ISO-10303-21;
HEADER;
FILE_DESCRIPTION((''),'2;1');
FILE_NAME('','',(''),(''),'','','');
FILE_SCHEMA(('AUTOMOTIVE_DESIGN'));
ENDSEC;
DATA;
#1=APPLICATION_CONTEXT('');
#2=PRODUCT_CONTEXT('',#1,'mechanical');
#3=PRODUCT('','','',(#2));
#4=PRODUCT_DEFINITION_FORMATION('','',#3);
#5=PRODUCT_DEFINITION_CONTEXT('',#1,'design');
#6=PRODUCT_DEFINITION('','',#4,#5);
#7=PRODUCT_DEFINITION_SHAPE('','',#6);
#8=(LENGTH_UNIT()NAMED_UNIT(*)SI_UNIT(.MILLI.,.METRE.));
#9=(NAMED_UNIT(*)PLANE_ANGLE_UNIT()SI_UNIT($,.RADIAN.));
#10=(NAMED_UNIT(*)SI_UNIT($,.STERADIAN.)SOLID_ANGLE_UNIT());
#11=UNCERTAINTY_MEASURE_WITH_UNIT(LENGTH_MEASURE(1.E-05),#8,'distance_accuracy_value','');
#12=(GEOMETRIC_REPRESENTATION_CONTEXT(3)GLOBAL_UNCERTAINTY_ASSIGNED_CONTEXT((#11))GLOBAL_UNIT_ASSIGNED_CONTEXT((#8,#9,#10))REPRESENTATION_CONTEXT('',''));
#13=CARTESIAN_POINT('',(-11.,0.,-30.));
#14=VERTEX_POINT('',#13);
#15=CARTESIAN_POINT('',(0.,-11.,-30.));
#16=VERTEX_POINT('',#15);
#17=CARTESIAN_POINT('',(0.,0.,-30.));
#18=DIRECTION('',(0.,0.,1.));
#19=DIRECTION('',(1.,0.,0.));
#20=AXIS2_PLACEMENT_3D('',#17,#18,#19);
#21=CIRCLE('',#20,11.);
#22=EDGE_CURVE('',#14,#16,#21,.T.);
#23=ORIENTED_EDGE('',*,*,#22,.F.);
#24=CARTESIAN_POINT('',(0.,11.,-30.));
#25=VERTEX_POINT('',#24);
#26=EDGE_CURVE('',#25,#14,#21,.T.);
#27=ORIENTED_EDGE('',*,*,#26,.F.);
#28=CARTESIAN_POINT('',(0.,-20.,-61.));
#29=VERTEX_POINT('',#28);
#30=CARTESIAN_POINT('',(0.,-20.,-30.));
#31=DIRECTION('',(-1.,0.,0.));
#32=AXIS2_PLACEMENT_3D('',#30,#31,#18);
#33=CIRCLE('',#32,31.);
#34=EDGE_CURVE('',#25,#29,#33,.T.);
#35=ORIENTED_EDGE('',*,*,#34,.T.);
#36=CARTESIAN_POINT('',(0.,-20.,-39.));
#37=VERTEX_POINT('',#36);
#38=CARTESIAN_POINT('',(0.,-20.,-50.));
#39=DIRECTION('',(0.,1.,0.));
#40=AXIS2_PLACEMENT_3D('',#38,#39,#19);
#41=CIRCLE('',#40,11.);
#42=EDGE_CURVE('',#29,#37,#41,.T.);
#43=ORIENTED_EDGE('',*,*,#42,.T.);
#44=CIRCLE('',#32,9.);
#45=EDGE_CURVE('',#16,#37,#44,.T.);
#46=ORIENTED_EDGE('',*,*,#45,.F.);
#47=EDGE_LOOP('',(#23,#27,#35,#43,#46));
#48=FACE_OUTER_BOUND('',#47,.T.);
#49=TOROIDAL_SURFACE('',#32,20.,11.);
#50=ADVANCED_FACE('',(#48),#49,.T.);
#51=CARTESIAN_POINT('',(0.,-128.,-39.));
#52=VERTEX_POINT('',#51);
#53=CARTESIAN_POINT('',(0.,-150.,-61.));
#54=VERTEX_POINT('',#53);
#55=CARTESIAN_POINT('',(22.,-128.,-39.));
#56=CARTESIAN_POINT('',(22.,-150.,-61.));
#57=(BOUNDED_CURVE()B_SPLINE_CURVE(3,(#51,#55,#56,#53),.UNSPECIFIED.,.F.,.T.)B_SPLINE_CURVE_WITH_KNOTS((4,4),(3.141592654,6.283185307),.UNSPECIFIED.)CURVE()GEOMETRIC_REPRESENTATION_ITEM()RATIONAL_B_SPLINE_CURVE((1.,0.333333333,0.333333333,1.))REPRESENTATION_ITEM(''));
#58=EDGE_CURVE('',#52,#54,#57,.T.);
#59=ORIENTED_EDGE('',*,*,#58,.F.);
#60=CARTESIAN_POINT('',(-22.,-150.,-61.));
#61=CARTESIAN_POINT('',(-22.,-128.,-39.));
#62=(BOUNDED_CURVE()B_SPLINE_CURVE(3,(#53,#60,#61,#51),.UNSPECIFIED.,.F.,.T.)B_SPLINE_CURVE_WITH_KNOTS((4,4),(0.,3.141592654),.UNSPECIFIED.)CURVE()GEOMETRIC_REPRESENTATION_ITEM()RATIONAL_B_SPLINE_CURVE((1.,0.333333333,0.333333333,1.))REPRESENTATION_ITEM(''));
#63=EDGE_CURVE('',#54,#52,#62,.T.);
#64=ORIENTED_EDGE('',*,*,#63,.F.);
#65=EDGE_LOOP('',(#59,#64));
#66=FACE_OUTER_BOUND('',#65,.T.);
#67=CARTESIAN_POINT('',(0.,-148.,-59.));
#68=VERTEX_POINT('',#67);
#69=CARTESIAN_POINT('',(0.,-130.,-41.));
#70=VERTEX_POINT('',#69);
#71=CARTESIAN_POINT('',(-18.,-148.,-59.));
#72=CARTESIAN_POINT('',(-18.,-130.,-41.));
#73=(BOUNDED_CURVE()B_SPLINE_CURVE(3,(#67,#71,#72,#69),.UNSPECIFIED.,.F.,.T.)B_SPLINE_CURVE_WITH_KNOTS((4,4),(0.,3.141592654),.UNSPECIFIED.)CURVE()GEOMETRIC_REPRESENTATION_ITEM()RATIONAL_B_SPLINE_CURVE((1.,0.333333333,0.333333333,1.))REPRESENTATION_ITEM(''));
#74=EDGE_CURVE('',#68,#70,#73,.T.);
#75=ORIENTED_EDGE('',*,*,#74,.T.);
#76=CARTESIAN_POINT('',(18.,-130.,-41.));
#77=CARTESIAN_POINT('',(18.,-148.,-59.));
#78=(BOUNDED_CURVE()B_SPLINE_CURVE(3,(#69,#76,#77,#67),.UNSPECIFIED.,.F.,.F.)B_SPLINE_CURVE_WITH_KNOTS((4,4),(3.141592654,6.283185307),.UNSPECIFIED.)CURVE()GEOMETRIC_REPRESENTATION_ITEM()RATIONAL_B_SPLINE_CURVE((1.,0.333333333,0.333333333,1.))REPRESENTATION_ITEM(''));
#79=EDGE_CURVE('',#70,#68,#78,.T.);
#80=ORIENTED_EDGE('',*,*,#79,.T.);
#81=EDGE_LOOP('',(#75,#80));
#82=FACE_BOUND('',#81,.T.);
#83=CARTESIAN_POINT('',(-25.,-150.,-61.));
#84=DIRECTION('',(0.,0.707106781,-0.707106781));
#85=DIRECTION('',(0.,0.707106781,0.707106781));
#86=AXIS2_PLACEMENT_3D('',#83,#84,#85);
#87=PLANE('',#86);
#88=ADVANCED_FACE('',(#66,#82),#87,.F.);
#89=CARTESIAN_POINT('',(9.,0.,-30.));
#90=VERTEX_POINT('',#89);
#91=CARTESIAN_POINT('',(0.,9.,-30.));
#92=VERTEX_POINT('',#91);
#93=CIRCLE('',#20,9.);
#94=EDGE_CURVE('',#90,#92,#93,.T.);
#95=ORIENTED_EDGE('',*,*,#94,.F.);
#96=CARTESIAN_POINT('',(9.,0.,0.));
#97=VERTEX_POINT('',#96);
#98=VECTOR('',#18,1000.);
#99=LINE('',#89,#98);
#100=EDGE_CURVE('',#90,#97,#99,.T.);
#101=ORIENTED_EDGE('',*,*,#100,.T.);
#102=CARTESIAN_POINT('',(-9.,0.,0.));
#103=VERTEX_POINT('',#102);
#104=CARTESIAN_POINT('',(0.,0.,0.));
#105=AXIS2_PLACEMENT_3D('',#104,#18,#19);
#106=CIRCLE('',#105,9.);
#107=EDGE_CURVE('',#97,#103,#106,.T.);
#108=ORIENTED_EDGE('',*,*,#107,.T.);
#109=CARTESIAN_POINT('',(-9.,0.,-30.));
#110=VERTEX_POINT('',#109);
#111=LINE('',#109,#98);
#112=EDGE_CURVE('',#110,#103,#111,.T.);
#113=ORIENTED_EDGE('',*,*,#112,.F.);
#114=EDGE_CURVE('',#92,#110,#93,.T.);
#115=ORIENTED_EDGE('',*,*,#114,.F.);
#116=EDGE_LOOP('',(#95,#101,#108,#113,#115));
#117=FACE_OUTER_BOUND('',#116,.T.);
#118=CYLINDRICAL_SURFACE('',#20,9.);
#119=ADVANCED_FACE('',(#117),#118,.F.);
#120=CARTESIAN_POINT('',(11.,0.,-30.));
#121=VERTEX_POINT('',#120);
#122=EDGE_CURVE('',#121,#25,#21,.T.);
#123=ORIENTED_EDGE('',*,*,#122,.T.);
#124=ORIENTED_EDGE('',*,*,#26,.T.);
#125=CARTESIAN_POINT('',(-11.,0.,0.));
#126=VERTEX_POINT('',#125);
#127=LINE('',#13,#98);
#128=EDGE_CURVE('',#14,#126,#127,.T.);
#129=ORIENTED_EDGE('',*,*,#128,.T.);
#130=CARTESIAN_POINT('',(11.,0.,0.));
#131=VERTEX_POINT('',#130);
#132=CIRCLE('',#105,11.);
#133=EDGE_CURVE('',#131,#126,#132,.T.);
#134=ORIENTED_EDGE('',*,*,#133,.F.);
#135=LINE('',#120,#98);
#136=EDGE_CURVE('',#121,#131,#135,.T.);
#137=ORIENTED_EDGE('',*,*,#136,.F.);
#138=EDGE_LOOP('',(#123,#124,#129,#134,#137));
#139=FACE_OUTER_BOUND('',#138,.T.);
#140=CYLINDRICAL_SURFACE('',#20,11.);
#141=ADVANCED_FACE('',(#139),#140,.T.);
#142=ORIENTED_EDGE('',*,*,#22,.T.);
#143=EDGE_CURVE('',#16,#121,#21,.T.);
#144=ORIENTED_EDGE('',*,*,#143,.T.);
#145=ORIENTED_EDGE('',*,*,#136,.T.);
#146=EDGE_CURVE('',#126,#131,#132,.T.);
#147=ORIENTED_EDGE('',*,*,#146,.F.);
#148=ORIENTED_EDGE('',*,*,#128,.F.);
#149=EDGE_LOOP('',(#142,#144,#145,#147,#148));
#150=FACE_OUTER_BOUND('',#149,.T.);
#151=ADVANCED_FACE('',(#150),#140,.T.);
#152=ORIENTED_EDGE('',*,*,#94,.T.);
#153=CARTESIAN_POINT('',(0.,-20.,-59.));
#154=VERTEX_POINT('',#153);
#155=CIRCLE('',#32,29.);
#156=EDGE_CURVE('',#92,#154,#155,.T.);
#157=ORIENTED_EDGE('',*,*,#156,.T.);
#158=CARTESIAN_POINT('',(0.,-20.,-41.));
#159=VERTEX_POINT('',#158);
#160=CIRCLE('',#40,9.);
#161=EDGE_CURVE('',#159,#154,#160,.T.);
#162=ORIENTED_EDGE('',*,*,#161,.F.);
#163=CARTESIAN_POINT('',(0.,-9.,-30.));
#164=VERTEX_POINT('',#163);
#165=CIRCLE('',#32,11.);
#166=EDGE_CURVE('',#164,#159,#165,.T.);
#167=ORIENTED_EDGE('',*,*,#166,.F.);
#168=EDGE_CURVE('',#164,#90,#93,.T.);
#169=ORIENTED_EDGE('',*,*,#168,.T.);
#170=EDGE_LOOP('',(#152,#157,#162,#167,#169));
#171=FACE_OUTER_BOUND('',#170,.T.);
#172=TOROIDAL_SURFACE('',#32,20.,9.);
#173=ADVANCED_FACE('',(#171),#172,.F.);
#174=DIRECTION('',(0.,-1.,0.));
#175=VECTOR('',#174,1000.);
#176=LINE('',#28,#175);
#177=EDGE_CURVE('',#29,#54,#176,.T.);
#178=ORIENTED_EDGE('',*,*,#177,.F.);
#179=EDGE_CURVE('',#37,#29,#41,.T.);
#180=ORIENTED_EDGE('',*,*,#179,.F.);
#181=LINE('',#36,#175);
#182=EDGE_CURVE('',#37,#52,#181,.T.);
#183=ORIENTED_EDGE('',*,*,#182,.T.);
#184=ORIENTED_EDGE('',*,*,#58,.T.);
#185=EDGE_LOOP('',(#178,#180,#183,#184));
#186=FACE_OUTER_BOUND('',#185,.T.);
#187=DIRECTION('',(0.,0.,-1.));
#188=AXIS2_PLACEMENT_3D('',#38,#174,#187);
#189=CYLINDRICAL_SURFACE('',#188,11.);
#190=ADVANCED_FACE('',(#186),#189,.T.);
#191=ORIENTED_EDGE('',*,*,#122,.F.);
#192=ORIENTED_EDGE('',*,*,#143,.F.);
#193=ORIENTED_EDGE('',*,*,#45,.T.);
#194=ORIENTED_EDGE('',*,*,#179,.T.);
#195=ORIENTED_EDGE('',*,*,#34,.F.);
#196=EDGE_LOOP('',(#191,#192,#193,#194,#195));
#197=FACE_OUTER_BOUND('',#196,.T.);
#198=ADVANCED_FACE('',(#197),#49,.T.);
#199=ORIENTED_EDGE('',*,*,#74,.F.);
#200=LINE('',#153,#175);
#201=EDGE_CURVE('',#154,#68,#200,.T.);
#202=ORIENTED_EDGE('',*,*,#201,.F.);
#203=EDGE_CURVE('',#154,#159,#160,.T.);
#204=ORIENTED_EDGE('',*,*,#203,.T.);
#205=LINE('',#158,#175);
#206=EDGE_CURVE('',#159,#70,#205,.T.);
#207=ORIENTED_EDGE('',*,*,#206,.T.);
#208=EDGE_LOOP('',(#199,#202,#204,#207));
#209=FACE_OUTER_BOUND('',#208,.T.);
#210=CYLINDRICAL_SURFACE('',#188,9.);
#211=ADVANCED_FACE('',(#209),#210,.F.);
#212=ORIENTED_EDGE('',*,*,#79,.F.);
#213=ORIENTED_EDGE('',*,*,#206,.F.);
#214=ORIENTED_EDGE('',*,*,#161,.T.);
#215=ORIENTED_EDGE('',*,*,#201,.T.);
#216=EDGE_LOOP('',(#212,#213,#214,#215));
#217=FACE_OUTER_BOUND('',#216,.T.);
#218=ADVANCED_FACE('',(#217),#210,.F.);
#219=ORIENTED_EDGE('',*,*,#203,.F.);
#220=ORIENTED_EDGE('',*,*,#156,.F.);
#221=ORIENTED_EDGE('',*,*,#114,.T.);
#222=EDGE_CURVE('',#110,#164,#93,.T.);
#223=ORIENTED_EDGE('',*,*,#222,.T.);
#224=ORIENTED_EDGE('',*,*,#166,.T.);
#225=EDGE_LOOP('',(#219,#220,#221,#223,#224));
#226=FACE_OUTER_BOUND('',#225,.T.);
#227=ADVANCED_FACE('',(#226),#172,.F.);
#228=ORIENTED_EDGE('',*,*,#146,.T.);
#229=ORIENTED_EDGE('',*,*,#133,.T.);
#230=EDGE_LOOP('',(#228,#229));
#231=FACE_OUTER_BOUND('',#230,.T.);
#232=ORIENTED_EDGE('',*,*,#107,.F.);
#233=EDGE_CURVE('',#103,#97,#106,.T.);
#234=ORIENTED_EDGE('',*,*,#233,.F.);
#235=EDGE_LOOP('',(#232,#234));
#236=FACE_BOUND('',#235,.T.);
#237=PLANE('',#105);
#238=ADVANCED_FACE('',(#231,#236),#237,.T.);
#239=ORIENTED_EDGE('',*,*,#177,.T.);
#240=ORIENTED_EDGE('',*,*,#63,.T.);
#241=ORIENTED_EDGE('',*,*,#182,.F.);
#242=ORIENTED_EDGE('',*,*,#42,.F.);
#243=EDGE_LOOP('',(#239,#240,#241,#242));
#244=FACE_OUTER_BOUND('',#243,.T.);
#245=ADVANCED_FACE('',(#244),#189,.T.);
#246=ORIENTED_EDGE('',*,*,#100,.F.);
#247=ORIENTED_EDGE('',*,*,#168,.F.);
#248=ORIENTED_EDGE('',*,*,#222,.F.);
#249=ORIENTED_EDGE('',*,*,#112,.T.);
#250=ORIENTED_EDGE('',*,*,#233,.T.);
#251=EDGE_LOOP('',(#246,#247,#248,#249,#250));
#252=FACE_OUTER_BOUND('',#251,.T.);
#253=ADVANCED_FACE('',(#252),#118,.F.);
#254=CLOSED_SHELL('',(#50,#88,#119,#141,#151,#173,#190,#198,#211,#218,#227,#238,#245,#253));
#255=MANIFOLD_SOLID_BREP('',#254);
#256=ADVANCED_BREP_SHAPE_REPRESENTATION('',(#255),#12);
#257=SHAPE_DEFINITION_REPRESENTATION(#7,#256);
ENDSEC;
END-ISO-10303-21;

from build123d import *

# Parameters (mm, degrees)
SKETCH1_R          = 11
SKETCH1_R_2        = 9
CUT_EXTRUDE1_DEPTH = 25


with BuildPart() as part:
    # Sweep1: sweep along a path in Sketch2
    with BuildLine(Plane(origin=(0, 0, 0), x_dir=(0, 0, -1), z_dir=(1, 0, 0))) as sweep1_path:
        Line((0, 0), (30, 0))
        ThreePointArc((30, 0), (44.142135624, -5.857864376), (50, -20))
        Line((50, -20), (50, -150))
    # Sketch1 → Sweep1 (sweep)
    with BuildSketch(Plane.XY):
        Circle(SKETCH1_R)
        Circle(SKETCH1_R_2, mode=Mode.SUBTRACT)
    sweep(path=sweep1_path.line)

    # Sketch3 → Cut-Extrude1 (cut, symmetric)
    with BuildSketch(Plane(origin=(0, 0, 0), x_dir=(0, 0, -1), z_dir=(1, 0, 0))):
        Polygon((61, -150), (36.244444784, -125.244444784), (36.244444784, -150), align=None)
    extrude(amount=CUT_EXTRUDE1_DEPTH, both=True, mode=Mode.SUBTRACT)


solid = part.part
